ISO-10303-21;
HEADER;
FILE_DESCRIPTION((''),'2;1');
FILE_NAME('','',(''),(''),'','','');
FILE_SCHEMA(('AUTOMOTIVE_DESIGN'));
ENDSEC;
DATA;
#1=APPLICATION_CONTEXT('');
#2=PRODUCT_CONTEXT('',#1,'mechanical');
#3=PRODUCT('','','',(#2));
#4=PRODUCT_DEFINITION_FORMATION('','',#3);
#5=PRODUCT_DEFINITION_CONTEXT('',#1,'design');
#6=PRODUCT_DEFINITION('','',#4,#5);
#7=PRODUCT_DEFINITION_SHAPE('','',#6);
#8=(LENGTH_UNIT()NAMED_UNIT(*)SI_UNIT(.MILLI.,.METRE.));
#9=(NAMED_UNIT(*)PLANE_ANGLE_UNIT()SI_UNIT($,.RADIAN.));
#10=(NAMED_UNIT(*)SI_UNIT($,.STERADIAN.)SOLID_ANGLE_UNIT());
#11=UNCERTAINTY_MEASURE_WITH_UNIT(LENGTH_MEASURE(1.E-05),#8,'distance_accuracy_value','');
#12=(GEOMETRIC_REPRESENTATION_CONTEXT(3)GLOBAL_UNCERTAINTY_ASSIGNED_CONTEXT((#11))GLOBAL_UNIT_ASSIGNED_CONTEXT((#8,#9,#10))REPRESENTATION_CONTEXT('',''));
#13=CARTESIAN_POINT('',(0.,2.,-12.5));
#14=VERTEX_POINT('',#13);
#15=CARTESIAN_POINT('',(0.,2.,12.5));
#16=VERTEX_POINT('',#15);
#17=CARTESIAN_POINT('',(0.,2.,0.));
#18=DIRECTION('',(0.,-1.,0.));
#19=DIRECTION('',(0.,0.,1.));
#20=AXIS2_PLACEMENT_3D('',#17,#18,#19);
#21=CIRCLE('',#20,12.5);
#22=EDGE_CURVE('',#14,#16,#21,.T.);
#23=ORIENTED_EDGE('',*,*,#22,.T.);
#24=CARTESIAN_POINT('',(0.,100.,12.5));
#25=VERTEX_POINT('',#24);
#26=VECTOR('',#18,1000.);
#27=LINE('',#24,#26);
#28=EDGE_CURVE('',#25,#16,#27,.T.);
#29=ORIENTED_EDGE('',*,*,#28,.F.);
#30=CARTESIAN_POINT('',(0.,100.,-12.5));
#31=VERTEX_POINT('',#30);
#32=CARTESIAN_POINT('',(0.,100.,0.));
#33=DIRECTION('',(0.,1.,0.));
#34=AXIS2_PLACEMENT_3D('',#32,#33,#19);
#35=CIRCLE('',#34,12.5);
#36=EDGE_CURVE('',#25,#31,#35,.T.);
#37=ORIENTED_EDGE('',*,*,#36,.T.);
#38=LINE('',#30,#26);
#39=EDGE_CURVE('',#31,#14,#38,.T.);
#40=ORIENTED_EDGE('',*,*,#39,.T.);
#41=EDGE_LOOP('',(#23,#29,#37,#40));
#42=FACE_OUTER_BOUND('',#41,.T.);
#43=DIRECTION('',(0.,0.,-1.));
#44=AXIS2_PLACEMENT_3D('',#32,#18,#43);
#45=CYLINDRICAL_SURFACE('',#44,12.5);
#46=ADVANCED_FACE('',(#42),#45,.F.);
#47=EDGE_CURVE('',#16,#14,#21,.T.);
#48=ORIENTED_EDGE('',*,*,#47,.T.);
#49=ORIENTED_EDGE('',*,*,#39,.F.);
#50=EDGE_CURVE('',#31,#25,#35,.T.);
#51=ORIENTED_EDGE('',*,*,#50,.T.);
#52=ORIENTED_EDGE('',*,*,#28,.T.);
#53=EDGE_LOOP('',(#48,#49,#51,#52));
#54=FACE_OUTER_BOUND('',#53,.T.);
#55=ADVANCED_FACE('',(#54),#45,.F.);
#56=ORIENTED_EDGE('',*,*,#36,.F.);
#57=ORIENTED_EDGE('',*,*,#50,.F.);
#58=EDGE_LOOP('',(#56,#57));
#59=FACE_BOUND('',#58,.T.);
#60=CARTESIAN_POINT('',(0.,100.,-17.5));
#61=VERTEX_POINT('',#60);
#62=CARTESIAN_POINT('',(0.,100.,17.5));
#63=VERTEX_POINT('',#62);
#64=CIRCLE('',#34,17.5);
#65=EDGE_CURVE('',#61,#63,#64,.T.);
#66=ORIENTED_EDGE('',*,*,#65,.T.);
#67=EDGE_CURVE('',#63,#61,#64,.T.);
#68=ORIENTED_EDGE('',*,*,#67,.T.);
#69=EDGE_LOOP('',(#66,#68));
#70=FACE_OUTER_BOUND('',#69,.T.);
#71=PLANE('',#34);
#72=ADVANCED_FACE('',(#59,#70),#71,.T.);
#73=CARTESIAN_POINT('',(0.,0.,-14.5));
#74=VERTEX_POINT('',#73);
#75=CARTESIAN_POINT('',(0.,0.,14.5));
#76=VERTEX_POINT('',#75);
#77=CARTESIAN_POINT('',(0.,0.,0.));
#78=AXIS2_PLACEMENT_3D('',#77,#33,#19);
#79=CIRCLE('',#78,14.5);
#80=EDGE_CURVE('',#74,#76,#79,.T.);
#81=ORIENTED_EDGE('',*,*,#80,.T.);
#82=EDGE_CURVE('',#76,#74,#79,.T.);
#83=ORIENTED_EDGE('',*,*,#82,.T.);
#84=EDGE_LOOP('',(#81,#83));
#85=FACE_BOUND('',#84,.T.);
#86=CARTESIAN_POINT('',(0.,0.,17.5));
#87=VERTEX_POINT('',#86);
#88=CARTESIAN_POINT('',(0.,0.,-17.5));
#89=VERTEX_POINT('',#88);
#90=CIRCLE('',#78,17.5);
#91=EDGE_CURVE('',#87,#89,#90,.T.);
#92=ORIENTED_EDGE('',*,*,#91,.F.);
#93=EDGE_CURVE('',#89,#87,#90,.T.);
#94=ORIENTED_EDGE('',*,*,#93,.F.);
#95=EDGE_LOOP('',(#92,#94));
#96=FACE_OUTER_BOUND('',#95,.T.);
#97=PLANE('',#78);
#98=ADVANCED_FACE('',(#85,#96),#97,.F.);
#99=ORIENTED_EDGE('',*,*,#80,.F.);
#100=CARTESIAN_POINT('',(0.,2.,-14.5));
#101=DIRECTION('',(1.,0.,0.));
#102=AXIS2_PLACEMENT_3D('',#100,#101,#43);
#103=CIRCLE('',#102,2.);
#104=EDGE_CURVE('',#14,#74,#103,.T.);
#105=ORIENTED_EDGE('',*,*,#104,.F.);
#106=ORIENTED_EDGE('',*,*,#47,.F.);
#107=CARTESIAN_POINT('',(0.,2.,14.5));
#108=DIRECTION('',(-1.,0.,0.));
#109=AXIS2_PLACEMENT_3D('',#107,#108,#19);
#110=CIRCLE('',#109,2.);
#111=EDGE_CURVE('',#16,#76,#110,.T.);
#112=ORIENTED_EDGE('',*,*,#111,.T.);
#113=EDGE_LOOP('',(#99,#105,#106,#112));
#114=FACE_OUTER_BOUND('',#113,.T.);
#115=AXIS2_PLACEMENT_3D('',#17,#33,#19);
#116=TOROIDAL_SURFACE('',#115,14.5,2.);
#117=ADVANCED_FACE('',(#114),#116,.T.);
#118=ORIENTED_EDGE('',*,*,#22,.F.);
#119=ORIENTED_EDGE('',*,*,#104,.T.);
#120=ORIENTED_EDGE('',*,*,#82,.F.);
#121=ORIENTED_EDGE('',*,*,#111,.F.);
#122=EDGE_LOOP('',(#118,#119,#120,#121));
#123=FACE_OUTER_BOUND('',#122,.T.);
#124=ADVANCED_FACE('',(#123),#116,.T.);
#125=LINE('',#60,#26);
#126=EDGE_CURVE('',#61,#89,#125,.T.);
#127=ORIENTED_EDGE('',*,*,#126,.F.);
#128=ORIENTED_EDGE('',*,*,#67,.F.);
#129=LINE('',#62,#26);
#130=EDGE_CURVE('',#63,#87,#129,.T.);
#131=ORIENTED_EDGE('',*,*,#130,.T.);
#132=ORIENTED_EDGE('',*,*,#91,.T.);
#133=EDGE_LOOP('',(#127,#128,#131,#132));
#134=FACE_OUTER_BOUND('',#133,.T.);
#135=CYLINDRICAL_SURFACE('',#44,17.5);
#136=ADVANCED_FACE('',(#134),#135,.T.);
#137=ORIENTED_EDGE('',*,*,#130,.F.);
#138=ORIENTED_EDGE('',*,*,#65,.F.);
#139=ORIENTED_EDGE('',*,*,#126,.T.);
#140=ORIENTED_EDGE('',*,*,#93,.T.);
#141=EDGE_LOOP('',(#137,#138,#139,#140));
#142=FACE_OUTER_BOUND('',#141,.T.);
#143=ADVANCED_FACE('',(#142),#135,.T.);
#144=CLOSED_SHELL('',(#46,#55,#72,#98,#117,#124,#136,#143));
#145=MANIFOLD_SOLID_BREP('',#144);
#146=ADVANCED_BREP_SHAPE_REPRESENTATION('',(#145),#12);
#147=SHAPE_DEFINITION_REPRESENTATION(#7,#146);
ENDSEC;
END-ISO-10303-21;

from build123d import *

# Parameters (mm, degrees)
SKETCH1_R           = 17.5
SKETCH1_R_2         = 12.5
BOSS_EXTRUDE1_DEPTH = 100
FILLET1_R           = 2


with BuildPart() as part:
    # Sketch1 → Boss-Extrude1 (new body)
    with BuildSketch(Plane(origin=(0, 0, 0), x_dir=(1, 0, 0), z_dir=(0, 1, 0))):
        with Locations(Location((0, 0, 0), (0, 0, 270))):
            Circle(SKETCH1_R)
        with Locations(Location((0, 0, 0), (0, 0, 270))):
            Circle(SKETCH1_R_2, mode=Mode.SUBTRACT)
    extrude(amount=BOSS_EXTRUDE1_DEPTH)

    # Fillet1
    fillet1_edges = [part.edges().sort_by_distance(p)[0] for p in [
        (0, 0, -12.5),
    ]]
    fillet(fillet1_edges, radius=FILLET1_R)


solid = part.part
